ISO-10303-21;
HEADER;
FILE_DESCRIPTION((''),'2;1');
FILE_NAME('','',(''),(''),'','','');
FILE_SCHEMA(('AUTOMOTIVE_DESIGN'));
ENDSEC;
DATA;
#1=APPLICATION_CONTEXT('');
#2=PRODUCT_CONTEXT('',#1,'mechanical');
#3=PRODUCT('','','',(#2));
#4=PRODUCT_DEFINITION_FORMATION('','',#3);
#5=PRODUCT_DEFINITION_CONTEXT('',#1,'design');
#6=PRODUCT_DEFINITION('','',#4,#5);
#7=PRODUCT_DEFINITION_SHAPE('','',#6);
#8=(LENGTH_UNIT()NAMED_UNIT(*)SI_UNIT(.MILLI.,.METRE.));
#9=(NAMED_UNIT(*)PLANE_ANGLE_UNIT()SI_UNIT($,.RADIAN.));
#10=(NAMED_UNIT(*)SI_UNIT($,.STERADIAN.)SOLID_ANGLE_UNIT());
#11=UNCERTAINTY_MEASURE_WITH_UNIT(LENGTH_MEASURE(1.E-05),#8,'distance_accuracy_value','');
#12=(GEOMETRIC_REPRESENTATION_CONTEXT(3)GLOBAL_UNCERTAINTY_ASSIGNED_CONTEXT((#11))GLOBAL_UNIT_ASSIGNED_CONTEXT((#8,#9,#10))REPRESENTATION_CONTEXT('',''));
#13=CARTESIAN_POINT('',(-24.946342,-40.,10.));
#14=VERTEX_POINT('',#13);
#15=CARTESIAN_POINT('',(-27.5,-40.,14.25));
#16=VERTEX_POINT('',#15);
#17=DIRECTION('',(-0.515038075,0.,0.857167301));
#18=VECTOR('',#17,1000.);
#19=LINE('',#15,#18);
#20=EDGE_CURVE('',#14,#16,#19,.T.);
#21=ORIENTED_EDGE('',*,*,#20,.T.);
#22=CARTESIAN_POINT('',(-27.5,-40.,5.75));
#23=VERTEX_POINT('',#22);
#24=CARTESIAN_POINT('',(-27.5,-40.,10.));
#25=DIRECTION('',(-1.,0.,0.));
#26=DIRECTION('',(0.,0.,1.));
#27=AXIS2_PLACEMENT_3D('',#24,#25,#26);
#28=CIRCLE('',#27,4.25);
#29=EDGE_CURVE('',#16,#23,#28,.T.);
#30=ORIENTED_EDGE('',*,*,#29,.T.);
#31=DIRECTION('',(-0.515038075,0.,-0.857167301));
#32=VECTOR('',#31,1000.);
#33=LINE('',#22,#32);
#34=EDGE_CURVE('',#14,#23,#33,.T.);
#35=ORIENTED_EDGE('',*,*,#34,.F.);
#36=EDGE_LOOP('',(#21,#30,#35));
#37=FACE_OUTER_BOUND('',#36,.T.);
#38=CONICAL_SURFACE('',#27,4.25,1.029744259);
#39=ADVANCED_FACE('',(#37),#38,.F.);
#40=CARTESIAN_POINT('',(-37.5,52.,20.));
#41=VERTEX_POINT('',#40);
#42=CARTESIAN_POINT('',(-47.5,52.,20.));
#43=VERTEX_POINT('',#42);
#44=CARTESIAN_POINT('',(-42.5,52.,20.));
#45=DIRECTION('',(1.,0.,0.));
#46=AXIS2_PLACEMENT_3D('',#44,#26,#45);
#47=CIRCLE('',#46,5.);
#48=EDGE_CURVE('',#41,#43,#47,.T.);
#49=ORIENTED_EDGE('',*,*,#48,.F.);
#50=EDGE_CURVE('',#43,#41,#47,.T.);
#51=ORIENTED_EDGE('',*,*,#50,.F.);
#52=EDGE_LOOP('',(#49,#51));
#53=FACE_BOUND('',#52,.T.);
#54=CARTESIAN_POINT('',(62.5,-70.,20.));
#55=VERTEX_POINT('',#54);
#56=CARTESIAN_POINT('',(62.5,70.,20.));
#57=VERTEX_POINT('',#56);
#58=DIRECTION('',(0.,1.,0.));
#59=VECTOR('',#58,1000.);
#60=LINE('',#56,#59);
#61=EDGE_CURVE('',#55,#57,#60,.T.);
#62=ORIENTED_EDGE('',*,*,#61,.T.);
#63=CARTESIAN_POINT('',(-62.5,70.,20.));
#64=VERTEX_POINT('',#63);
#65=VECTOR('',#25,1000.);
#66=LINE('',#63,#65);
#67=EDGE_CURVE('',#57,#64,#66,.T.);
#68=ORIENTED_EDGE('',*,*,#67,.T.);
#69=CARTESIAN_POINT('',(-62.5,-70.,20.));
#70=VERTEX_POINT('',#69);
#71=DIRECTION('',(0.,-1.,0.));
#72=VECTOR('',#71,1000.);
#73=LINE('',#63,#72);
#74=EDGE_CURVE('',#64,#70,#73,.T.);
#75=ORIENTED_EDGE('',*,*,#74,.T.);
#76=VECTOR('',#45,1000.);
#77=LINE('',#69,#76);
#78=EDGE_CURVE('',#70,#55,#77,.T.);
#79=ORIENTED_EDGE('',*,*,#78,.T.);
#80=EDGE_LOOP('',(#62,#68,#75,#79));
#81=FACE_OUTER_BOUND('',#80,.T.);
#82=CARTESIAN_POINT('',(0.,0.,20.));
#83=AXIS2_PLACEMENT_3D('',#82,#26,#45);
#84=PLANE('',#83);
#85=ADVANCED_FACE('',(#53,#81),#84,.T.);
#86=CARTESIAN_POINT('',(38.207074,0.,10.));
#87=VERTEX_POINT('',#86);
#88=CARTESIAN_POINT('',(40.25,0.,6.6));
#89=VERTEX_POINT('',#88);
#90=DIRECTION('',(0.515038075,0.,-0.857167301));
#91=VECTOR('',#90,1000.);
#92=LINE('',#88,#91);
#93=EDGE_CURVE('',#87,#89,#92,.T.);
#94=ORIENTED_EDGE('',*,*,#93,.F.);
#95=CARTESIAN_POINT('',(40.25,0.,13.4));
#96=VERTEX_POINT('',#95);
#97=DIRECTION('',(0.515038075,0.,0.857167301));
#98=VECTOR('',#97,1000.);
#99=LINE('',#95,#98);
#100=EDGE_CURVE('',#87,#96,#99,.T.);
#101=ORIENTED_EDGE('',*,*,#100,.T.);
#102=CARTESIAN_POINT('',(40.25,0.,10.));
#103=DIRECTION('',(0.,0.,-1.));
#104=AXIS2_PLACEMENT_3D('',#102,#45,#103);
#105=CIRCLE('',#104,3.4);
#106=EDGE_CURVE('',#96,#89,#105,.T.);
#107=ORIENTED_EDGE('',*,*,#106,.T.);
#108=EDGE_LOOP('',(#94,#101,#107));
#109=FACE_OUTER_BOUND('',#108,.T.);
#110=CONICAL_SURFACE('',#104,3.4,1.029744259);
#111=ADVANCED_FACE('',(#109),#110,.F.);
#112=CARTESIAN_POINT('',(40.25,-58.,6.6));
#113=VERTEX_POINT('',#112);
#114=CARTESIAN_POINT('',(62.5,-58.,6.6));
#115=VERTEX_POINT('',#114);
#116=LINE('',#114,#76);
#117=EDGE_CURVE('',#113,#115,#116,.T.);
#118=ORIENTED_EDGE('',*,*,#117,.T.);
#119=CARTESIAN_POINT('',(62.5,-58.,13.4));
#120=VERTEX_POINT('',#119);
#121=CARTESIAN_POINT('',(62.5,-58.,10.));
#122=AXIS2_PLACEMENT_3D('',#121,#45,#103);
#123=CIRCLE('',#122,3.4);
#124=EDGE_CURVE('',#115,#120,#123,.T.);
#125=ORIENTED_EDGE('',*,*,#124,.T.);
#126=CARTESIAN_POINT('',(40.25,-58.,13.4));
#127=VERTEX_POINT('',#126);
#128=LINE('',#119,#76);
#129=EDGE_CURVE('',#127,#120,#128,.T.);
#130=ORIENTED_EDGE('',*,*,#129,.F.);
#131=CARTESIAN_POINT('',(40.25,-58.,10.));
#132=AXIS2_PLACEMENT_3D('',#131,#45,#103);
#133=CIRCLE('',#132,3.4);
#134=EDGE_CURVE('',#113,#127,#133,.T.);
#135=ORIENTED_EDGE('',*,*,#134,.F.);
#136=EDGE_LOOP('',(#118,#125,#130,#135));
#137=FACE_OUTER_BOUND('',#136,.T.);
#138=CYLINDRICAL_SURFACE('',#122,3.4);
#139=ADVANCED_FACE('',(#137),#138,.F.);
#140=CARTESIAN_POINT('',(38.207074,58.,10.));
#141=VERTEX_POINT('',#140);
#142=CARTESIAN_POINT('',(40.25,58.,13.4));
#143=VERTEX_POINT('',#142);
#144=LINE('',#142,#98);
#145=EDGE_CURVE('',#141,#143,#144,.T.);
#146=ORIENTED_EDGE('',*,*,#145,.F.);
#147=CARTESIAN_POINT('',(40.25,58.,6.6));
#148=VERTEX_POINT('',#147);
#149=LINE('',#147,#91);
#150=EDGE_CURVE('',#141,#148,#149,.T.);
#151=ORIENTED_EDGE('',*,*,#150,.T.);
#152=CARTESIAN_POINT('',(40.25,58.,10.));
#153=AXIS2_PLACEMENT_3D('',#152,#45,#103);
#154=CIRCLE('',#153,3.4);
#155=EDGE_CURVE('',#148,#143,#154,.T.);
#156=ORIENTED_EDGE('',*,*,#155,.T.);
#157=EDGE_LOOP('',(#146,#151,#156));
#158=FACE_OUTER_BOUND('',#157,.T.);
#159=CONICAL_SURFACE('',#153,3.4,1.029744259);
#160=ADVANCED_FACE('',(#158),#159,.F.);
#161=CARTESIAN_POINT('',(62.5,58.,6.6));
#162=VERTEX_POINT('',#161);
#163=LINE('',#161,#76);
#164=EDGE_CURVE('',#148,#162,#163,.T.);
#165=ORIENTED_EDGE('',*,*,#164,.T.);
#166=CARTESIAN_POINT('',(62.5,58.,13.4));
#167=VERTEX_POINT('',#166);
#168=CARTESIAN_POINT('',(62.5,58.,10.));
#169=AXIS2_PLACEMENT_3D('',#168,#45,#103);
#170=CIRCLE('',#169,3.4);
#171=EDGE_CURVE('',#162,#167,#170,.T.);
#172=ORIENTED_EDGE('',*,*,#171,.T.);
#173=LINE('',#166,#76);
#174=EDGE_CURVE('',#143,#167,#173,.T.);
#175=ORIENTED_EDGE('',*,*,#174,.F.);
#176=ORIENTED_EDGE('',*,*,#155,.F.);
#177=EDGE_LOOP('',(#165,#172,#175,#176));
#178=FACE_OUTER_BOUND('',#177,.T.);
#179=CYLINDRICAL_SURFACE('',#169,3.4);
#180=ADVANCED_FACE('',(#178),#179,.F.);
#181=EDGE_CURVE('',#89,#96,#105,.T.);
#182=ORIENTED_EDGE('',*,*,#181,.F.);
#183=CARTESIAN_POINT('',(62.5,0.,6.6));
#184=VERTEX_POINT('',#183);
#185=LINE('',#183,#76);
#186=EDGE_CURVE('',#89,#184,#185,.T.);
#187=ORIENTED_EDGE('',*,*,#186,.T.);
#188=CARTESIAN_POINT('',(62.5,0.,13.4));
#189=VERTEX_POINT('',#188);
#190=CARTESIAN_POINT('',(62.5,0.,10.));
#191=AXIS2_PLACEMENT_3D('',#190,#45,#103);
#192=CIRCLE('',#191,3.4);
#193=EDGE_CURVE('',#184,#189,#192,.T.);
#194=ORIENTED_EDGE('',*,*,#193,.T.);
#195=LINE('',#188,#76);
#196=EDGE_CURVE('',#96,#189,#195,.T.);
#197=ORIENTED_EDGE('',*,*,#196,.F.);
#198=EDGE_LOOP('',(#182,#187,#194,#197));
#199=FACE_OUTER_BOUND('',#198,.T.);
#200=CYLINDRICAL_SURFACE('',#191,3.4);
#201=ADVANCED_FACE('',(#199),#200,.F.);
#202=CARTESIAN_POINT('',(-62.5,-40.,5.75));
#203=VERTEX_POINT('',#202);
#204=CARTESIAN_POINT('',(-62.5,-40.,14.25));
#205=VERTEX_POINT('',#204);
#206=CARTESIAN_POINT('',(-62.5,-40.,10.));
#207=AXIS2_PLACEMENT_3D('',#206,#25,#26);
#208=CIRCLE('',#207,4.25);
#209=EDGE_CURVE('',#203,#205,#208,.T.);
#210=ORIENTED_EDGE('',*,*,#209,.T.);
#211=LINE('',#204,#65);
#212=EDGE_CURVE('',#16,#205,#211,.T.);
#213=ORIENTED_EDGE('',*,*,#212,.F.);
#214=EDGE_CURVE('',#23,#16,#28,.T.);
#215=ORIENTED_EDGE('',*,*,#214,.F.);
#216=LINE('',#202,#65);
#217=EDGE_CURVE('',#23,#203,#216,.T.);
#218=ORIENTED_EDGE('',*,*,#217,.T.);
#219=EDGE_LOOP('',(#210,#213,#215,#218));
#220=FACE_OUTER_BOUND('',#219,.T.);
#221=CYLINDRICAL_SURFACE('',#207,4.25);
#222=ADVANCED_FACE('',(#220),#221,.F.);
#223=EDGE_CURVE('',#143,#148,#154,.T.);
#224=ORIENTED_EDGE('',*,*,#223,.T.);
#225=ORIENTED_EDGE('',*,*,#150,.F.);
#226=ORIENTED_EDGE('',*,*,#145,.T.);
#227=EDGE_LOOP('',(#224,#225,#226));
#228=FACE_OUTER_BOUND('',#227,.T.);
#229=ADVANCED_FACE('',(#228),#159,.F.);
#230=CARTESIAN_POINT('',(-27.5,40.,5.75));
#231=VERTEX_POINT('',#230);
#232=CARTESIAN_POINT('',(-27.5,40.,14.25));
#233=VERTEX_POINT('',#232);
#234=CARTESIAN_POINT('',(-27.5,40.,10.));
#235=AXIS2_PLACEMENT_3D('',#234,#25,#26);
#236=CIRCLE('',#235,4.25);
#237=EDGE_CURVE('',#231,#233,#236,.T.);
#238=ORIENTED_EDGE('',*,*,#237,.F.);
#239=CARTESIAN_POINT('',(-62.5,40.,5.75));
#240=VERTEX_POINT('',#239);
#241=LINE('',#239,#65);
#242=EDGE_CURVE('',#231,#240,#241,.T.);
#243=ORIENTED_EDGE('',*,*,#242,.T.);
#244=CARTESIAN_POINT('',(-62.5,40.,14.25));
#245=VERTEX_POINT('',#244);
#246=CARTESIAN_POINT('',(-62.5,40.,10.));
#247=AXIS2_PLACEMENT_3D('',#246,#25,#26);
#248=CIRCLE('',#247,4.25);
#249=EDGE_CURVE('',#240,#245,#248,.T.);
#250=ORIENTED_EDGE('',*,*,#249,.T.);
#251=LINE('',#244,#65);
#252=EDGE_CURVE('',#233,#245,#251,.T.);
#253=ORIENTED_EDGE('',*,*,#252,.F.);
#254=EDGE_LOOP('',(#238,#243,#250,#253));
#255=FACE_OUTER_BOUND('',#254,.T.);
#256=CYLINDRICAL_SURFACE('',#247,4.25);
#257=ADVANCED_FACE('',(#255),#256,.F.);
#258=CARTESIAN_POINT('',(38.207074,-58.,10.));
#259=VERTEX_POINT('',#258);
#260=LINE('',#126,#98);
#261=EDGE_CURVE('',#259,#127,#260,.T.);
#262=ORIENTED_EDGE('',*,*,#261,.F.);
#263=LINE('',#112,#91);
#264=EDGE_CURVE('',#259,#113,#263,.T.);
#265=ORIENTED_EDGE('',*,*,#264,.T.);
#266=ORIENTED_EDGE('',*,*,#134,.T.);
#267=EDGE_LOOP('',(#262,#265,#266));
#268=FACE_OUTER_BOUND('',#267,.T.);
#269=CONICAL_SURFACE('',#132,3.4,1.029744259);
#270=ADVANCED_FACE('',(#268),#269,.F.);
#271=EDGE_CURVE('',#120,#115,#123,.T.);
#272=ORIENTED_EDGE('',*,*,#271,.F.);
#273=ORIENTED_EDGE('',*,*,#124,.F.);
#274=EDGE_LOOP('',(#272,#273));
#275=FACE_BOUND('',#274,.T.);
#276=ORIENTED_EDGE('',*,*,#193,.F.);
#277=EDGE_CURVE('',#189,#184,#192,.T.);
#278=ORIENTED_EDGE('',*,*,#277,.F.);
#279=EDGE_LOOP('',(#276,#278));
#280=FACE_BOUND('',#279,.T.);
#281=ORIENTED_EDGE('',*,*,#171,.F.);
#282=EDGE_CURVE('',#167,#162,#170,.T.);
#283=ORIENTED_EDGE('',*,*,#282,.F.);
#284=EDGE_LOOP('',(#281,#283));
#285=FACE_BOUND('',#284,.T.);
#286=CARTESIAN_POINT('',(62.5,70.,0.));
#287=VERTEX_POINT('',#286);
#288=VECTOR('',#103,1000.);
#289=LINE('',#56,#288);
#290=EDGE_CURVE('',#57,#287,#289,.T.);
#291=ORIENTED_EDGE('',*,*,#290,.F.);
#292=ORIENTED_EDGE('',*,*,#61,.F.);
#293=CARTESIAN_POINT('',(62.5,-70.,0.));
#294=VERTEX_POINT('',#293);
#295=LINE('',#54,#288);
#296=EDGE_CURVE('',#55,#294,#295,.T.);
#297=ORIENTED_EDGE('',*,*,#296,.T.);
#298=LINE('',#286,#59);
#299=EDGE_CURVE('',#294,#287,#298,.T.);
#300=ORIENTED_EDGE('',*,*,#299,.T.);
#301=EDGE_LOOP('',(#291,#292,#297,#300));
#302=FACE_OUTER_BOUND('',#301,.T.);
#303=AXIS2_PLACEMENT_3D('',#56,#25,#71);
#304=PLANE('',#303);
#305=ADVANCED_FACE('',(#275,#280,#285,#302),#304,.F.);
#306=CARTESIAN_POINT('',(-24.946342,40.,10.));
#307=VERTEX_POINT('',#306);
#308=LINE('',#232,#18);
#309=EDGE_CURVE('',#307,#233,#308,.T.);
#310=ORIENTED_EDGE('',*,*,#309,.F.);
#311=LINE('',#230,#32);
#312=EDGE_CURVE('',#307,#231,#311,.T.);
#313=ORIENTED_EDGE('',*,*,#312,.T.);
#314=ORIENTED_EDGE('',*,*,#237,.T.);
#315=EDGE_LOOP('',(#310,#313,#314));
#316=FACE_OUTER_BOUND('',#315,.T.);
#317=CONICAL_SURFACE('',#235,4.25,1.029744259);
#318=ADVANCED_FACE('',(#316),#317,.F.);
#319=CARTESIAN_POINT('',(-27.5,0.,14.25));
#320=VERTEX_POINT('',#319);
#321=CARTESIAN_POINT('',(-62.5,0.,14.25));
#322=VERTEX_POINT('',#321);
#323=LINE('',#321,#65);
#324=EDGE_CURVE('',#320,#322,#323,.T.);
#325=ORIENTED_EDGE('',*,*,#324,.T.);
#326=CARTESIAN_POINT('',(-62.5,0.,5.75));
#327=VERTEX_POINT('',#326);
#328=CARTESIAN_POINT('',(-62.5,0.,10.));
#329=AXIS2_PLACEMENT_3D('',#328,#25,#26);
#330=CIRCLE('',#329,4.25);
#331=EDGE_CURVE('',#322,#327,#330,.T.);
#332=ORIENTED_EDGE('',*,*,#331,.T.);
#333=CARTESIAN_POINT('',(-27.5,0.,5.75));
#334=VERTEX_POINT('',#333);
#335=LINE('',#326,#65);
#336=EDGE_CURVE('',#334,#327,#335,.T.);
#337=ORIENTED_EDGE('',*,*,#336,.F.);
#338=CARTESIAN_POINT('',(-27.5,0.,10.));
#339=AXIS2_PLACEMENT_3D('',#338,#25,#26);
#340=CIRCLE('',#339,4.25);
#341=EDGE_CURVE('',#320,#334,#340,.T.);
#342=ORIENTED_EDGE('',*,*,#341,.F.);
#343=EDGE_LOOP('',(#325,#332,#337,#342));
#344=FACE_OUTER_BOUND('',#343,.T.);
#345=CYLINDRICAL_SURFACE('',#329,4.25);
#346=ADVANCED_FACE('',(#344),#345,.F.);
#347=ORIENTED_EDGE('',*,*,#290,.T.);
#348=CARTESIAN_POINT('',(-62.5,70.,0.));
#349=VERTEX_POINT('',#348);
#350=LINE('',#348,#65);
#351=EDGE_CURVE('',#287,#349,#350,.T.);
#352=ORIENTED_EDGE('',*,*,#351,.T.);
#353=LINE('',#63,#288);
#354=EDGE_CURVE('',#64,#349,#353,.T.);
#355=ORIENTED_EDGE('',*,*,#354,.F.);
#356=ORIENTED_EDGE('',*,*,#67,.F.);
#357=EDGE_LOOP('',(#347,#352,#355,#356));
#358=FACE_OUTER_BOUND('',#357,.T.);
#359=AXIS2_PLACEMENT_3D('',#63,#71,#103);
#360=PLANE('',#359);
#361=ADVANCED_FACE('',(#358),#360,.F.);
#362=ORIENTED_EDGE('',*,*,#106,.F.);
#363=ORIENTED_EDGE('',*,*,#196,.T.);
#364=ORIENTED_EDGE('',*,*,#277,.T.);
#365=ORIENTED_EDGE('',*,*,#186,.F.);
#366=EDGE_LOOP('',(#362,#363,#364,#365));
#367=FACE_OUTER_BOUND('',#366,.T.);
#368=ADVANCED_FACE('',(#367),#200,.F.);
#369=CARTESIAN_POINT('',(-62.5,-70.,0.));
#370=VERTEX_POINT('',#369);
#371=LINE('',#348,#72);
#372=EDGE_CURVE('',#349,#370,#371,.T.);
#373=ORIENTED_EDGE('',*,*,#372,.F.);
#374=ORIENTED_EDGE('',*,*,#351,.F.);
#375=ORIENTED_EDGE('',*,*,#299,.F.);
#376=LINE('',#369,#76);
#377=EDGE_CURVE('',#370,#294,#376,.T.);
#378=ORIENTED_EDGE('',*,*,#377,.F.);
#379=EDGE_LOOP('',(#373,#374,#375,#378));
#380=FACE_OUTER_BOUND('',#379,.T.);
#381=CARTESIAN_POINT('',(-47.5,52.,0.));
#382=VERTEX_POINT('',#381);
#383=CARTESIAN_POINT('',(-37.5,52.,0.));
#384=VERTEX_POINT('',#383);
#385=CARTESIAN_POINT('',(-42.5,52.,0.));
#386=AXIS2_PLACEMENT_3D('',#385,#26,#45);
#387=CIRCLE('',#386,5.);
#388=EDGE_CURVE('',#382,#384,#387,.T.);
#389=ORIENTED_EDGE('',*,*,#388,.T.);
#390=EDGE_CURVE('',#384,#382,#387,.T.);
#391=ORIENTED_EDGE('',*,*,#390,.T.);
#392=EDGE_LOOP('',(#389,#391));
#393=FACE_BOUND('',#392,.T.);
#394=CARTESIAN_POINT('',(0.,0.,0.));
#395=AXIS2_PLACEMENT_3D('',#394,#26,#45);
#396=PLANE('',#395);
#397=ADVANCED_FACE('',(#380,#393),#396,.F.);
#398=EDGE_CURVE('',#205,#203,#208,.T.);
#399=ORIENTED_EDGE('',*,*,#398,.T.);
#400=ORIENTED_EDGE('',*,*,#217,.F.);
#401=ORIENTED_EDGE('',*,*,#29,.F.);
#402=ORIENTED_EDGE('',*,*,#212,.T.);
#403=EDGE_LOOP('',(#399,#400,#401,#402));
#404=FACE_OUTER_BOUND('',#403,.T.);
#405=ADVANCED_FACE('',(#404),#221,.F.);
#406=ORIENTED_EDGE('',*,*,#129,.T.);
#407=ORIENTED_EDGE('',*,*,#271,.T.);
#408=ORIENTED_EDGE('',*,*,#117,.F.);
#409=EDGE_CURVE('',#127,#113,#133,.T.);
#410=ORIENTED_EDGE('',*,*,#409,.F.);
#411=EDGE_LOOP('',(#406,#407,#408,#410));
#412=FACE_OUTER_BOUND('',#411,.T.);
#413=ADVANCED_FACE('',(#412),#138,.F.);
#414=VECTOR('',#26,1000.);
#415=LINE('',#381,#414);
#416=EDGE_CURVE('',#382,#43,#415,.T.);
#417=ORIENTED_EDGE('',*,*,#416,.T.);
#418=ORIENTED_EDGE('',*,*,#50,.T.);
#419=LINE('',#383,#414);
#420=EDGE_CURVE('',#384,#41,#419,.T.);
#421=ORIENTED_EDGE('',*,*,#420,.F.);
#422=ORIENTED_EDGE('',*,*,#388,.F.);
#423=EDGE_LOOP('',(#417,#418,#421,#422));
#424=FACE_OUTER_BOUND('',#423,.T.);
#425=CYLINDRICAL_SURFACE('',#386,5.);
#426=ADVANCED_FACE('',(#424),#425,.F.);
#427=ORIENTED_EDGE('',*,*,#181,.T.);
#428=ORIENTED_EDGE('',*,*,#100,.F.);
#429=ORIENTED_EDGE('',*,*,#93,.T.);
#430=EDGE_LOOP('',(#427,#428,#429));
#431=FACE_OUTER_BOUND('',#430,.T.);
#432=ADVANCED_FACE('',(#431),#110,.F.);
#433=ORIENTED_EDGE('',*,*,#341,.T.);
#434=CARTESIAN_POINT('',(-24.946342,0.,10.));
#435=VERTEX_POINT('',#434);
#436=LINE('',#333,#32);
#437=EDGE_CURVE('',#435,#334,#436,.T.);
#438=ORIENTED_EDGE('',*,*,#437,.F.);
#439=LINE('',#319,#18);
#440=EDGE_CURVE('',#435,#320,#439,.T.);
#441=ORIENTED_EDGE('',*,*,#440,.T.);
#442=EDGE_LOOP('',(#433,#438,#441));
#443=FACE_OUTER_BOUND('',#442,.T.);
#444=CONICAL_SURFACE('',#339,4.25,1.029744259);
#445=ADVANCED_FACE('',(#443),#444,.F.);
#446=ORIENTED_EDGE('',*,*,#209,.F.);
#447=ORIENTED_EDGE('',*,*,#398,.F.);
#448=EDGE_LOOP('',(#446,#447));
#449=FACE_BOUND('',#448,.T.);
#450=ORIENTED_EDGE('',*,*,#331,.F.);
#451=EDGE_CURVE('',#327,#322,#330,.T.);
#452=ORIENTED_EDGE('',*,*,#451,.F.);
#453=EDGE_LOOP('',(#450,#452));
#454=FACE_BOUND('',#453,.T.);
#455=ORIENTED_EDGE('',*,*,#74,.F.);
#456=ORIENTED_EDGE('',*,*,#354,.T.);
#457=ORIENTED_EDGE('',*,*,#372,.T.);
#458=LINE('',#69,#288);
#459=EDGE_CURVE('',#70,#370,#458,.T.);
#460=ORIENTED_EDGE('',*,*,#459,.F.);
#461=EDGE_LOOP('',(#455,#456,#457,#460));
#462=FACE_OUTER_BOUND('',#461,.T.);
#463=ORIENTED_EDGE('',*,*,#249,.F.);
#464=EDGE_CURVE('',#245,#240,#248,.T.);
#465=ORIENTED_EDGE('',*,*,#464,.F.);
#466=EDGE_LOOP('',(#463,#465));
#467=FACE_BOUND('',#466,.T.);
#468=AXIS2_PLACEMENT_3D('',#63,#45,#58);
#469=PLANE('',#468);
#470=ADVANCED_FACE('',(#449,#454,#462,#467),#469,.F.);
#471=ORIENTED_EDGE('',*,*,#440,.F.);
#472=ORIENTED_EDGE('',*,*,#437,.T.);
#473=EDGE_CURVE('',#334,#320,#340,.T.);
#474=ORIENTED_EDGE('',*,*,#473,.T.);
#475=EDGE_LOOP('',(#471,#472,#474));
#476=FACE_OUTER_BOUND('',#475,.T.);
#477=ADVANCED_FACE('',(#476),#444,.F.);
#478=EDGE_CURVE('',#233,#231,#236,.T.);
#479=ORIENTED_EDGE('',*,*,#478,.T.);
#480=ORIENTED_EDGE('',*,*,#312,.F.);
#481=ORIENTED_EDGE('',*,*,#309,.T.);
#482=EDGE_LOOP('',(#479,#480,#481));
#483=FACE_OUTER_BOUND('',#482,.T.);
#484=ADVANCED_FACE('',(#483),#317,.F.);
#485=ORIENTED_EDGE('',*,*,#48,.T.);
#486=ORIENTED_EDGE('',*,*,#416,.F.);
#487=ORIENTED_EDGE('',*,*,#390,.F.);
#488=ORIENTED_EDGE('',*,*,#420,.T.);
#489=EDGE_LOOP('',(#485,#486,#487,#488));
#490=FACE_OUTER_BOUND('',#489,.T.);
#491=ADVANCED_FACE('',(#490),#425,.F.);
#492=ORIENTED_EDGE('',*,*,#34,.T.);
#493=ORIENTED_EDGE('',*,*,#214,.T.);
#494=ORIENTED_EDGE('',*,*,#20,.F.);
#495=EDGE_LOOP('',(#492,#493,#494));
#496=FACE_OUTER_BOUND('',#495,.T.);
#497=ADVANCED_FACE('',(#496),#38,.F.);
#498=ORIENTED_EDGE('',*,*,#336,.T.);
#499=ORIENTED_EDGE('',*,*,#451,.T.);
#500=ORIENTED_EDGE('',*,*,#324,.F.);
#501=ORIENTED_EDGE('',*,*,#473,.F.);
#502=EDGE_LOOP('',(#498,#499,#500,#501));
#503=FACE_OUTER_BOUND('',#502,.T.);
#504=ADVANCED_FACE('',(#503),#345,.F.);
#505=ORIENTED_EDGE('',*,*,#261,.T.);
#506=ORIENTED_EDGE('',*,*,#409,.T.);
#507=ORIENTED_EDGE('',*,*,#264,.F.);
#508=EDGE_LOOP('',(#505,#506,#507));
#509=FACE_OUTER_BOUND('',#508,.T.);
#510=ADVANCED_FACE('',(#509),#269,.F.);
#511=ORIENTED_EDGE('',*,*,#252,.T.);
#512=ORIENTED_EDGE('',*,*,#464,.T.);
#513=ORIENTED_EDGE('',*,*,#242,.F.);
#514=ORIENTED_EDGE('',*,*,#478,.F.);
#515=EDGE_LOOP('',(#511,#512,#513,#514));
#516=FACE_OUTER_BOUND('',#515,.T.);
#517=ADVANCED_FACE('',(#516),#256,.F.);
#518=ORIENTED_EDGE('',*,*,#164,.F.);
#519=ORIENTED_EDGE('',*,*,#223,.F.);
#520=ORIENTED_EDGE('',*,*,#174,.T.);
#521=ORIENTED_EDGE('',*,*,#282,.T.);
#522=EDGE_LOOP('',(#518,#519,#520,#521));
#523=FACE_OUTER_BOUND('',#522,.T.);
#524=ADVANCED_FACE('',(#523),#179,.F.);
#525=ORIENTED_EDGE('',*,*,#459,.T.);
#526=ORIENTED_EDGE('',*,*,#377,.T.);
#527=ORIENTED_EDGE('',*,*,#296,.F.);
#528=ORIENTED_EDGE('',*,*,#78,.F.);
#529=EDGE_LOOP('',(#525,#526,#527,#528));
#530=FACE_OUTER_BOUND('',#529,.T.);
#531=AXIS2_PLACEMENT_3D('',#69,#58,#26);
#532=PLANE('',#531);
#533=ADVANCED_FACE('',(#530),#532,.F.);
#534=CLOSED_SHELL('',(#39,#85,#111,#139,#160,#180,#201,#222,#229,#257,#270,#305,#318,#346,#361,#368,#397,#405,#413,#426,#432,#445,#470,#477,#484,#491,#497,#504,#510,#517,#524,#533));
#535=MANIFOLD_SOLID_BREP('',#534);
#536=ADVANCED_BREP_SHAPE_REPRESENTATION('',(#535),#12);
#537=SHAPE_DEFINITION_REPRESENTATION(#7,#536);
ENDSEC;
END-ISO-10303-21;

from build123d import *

# Parameters (mm, degrees)
SKETCH1_W              = 125
SKETCH1_H              = 140
BOSS_EXTRUDE1_DEPTH    = 20
M10_TAPPED_HOLE1_D     = 8.5
M10_TAPPED_HOLE1_DEPTH = 35
M10_TAPPED_HOLE1_TIP   = 2.553657631
M8_TAPPED_HOLE1_D      = 6.8
M8_TAPPED_HOLE1_DEPTH  = 22.25
M8_TAPPED_HOLE1_TIP    = 2.042926105
SKETCH6_R              = 5
CUT_EXTRUDE1_DEPTH     = 96.949205312


with BuildPart() as part:
    # Sketch1 → Boss-Extrude1 (new body)
    with BuildSketch(Plane.XY):
        Rectangle(SKETCH1_W, SKETCH1_H)
    extrude(amount=BOSS_EXTRUDE1_DEPTH)

    # M10 Tapped Hole1
    with Locations(Plane.ZY.offset(62.5)):
        with Locations((10, 40), (10, 0), (10, -40)):
            Hole(M10_TAPPED_HOLE1_D / 2, depth=M10_TAPPED_HOLE1_DEPTH)
            with Locations((0, 0, -(M10_TAPPED_HOLE1_DEPTH + M10_TAPPED_HOLE1_TIP / 2))):  # 118° drill point
                Cone(0, M10_TAPPED_HOLE1_D / 2, M10_TAPPED_HOLE1_TIP, mode=Mode.SUBTRACT)

    # M8 Tapped Hole1
    with Locations(Plane(origin=(62.5, 0, 0), x_dir=(0, 0, -1), z_dir=(1, 0, 0))):
        with Locations((-10, 58), (-10, 0), (-10, -58)):
            Hole(M8_TAPPED_HOLE1_D / 2, depth=M8_TAPPED_HOLE1_DEPTH)
            with Locations((0, 0, -(M8_TAPPED_HOLE1_DEPTH + M8_TAPPED_HOLE1_TIP / 2))):  # 118° drill point
                Cone(0, M8_TAPPED_HOLE1_D / 2, M8_TAPPED_HOLE1_TIP, mode=Mode.SUBTRACT)

    # Sketch6 → Cut-Extrude1 (cut, through all)
    with BuildSketch(Plane.XY.offset(20)):
        with Locations((-42.5, 52)):
            Circle(SKETCH6_R)
    extrude(amount=-CUT_EXTRUDE1_DEPTH, mode=Mode.SUBTRACT)


solid = part.part
